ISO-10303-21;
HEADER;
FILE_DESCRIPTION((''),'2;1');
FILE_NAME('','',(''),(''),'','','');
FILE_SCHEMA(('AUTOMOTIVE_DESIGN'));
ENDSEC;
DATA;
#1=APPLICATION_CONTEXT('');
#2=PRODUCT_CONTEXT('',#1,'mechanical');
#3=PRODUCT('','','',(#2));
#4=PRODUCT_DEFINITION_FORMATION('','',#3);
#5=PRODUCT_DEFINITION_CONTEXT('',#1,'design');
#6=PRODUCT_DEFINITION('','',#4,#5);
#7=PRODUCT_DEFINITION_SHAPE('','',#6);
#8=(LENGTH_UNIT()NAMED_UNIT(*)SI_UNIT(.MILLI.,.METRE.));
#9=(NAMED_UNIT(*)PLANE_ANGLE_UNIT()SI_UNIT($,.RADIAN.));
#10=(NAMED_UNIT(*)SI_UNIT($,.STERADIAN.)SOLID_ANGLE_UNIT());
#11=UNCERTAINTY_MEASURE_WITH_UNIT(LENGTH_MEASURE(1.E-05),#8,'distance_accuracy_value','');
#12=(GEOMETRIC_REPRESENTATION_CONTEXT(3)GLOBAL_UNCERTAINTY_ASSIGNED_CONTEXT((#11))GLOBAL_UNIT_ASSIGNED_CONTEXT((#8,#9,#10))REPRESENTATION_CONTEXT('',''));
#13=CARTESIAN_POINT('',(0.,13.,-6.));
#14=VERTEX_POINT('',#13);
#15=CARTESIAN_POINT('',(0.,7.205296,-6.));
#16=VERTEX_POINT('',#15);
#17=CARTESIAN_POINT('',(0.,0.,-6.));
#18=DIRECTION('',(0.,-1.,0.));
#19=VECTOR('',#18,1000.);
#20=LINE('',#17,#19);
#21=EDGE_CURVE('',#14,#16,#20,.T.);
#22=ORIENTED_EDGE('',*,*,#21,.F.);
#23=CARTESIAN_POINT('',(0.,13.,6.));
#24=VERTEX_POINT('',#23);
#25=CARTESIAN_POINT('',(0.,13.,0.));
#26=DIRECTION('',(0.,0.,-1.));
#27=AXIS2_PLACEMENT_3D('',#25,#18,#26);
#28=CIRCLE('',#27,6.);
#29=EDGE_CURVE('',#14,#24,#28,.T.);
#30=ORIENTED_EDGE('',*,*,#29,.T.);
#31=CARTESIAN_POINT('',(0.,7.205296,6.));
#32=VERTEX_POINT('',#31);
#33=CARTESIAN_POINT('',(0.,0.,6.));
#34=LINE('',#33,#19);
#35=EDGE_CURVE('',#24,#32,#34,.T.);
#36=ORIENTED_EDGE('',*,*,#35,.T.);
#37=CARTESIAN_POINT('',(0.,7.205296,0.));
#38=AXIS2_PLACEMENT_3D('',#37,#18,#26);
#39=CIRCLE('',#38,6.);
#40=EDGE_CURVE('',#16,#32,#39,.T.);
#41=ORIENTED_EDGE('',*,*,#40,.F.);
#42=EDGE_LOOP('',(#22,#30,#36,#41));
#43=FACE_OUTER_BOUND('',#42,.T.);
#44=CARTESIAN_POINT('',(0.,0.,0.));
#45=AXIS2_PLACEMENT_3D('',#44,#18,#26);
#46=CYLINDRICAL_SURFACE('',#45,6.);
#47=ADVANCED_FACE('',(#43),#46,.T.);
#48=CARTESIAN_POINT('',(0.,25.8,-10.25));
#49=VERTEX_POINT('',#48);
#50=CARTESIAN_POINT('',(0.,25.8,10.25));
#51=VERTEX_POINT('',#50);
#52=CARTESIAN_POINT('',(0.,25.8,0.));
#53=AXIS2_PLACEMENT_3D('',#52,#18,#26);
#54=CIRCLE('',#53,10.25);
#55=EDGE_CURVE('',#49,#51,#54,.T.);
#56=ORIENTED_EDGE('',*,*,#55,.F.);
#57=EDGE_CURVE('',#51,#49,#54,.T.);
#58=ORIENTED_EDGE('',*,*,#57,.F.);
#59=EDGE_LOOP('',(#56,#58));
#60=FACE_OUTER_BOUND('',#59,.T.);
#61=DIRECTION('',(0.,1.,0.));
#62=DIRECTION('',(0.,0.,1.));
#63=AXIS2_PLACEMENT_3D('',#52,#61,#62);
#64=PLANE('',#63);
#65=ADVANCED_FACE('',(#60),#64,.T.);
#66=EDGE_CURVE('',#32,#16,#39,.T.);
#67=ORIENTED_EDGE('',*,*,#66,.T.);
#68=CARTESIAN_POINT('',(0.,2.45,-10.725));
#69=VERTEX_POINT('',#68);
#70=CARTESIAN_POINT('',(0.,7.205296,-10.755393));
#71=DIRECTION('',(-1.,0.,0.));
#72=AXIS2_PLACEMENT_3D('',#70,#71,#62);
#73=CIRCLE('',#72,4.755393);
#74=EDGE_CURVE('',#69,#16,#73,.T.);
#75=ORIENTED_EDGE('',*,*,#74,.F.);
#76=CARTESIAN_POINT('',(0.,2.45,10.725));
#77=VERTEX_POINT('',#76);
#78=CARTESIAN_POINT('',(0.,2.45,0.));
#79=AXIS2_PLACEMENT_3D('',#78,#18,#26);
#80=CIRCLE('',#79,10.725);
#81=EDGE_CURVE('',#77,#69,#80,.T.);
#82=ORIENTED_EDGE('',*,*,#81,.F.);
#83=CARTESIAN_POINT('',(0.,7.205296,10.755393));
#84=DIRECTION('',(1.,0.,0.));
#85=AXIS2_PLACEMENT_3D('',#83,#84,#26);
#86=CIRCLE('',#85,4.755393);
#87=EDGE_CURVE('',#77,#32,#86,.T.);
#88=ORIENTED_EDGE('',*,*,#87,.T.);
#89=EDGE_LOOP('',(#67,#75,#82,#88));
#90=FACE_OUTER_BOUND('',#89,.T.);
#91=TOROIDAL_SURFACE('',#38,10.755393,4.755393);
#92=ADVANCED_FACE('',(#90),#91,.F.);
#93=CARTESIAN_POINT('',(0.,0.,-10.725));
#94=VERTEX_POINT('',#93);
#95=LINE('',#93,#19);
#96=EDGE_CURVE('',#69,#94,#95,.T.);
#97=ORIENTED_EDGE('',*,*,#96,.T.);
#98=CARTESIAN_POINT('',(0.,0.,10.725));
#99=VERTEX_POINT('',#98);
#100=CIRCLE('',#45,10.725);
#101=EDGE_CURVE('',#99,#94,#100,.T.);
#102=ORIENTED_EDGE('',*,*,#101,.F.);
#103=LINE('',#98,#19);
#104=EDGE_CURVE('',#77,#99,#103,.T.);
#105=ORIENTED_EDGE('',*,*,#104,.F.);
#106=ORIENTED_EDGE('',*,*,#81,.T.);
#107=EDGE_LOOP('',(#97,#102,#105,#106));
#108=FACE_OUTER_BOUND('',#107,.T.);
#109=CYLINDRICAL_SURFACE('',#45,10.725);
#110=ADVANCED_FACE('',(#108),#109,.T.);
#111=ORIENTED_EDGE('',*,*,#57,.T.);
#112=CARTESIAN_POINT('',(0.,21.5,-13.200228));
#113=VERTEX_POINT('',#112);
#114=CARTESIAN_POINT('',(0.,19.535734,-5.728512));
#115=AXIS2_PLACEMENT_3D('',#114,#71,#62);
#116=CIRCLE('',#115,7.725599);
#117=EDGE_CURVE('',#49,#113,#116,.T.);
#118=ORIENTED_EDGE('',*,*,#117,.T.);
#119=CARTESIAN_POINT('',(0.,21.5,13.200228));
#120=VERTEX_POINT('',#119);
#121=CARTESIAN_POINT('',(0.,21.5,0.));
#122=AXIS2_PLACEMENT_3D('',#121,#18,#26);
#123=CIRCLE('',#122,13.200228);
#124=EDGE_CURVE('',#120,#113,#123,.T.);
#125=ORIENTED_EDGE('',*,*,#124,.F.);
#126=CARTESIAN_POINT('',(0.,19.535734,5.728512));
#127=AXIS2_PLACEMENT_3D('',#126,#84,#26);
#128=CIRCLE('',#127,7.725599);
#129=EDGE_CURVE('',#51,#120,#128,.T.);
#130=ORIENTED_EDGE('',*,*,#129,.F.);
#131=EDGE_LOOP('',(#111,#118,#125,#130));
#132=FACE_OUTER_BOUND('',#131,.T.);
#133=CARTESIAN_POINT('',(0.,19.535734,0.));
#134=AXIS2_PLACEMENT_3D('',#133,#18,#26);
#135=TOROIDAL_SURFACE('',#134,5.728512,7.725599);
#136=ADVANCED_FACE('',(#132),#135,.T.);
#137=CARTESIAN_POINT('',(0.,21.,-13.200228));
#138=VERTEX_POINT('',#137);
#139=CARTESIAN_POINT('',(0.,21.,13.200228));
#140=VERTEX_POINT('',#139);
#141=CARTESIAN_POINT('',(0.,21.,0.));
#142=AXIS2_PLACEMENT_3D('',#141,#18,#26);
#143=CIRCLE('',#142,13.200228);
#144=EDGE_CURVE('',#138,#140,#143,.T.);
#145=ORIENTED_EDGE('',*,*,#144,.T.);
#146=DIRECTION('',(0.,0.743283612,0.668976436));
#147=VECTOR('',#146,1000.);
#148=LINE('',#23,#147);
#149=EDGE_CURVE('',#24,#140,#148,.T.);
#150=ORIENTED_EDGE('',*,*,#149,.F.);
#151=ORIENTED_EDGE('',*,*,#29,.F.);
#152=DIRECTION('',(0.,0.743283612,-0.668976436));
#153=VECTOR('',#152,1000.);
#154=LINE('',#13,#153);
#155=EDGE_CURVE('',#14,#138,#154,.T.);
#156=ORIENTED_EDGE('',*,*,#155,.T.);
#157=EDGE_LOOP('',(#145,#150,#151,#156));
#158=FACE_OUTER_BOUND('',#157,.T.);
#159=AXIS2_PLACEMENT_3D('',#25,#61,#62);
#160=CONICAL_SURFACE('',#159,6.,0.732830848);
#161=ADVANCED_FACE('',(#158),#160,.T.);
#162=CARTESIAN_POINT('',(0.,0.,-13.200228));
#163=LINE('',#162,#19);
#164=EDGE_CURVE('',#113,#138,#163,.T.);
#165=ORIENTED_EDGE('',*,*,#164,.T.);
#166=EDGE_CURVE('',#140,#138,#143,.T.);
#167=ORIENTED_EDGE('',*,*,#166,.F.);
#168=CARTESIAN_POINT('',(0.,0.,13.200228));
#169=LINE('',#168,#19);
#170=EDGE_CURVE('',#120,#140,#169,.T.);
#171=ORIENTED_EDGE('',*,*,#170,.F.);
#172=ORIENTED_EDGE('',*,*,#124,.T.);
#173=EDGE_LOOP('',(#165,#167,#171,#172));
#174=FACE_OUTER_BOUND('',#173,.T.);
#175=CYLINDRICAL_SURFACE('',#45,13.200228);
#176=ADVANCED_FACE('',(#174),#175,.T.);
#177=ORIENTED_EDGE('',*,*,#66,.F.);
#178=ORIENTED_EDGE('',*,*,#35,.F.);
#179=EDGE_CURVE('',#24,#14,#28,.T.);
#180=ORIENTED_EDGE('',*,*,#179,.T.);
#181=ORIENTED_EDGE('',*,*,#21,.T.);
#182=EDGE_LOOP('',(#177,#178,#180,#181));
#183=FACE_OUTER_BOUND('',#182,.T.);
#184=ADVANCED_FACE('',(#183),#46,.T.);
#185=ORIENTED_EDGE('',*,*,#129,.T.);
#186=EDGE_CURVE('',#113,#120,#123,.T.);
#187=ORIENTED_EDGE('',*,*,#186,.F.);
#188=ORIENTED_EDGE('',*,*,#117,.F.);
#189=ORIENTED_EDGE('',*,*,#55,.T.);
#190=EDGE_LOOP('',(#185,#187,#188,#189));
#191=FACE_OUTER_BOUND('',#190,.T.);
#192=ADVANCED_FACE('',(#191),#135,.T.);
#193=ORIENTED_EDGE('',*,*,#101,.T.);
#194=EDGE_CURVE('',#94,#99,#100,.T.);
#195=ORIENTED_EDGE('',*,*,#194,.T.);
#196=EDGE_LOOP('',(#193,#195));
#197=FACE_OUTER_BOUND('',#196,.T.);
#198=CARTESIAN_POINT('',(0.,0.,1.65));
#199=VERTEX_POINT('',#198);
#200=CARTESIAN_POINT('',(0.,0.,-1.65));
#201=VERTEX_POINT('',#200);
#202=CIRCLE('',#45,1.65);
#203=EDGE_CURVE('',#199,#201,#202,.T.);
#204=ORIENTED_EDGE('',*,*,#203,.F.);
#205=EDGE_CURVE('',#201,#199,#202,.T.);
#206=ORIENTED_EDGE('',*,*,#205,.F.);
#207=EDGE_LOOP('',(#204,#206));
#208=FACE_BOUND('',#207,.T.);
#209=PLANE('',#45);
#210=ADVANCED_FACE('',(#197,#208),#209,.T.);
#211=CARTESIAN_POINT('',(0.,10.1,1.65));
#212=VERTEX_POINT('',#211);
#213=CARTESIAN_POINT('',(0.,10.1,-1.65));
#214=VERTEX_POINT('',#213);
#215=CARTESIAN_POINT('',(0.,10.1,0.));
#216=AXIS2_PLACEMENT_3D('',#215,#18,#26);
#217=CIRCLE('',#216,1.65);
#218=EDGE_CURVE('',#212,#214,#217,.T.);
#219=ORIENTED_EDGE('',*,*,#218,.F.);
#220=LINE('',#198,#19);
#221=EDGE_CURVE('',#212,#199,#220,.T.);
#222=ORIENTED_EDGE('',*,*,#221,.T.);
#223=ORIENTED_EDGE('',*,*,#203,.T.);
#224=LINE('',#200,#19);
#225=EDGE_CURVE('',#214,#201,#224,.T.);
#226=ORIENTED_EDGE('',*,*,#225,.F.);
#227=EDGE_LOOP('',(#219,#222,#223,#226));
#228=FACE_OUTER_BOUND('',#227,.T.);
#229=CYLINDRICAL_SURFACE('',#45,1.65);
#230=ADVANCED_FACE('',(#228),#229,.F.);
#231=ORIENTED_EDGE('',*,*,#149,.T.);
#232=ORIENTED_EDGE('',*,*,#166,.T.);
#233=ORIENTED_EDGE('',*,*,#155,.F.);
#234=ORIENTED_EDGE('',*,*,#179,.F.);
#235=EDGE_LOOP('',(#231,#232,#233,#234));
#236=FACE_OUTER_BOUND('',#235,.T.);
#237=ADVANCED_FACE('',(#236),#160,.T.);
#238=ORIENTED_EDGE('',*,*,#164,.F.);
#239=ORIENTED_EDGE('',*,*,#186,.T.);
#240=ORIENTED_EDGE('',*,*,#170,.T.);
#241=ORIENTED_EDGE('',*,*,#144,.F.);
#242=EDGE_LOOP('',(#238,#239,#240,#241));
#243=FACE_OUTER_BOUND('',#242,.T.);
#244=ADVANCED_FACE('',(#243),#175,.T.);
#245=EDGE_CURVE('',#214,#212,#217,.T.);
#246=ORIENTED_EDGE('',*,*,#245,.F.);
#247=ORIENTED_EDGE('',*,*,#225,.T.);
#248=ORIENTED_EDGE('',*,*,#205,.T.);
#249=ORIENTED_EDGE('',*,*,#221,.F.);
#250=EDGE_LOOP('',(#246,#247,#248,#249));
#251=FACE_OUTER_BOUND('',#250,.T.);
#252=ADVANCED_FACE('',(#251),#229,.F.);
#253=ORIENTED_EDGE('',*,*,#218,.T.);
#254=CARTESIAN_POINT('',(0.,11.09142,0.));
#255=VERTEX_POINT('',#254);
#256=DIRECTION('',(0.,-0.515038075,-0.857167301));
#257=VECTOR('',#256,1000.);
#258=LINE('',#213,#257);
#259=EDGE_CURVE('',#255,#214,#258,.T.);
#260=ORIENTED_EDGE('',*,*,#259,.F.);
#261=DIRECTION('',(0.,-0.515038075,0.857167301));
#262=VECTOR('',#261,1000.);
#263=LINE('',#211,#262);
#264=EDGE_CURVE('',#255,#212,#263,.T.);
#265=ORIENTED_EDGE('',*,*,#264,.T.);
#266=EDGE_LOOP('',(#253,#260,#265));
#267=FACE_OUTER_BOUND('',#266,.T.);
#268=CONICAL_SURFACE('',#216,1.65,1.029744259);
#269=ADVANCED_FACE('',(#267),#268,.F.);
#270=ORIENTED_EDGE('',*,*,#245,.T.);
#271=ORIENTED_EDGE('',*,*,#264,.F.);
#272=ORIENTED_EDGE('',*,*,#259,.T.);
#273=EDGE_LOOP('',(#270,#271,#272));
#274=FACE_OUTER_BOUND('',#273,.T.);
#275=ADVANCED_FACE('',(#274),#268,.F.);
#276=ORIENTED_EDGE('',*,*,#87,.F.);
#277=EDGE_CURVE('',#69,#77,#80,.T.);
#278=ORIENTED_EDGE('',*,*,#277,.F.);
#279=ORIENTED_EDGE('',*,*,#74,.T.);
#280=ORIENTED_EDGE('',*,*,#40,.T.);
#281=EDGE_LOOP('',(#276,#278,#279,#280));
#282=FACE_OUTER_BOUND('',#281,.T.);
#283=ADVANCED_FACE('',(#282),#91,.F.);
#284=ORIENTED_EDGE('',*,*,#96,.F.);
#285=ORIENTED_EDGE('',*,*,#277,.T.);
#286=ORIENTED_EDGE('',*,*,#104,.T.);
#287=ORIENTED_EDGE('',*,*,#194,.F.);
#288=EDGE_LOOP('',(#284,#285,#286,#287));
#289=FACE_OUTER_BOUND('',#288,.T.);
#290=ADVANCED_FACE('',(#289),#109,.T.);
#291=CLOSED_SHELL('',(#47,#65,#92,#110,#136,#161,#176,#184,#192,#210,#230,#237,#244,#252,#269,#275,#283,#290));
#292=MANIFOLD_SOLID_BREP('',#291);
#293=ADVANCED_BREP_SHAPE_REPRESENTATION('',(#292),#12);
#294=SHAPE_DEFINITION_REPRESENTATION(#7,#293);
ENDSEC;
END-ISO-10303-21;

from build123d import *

# Parameters (mm, degrees)
M4_TAPPED_HOLE1_D     = 3.3
M4_TAPPED_HOLE1_DEPTH = 10.1
M4_TAPPED_HOLE1_TIP   = 0.991420021


with BuildPart() as part:
    # Sketch1 → Revolve1 (revolve)
    with BuildSketch(Plane(origin=(0, 0, 0), x_dir=(0, 0, -1), z_dir=(1, 0, 0))):
        with BuildLine():
            Line((0, 0), (10.725, 0))
            Line((10.725, 0), (10.725, 2.45))
            ThreePointArc((10.725, 2.45), (7.382093902, 3.853488302), (6, 7.205296327))
            Line((6, 7.205296327), (6, 13))
            Line((6, 13), (13.200228011, 21))
            Line((13.200228011, 21), (13.200228011, 21.5))
            ThreePointArc((13.200228011, 21.5), (12.098891552, 23.906448602), (10.25, 25.8))
            Line((10.25, 25.8), (0, 25.8))
            Line((0, 25.8), (0, 0))
        make_face()
    revolve(axis=Axis((0, 0, 0), (0, 1, 0)))

    # M4 Tapped Hole1
    with Locations(Plane(origin=(0, 0, 0), x_dir=(-1, 0, 0), z_dir=(0, -1, 0))):
        with Locations((0, 0)):
            Hole(M4_TAPPED_HOLE1_D / 2, depth=M4_TAPPED_HOLE1_DEPTH)
            with Locations((0, 0, -(M4_TAPPED_HOLE1_DEPTH + M4_TAPPED_HOLE1_TIP / 2))):  # 118° drill point
                Cone(0, M4_TAPPED_HOLE1_D / 2, M4_TAPPED_HOLE1_TIP, mode=Mode.SUBTRACT)


solid = part.part
